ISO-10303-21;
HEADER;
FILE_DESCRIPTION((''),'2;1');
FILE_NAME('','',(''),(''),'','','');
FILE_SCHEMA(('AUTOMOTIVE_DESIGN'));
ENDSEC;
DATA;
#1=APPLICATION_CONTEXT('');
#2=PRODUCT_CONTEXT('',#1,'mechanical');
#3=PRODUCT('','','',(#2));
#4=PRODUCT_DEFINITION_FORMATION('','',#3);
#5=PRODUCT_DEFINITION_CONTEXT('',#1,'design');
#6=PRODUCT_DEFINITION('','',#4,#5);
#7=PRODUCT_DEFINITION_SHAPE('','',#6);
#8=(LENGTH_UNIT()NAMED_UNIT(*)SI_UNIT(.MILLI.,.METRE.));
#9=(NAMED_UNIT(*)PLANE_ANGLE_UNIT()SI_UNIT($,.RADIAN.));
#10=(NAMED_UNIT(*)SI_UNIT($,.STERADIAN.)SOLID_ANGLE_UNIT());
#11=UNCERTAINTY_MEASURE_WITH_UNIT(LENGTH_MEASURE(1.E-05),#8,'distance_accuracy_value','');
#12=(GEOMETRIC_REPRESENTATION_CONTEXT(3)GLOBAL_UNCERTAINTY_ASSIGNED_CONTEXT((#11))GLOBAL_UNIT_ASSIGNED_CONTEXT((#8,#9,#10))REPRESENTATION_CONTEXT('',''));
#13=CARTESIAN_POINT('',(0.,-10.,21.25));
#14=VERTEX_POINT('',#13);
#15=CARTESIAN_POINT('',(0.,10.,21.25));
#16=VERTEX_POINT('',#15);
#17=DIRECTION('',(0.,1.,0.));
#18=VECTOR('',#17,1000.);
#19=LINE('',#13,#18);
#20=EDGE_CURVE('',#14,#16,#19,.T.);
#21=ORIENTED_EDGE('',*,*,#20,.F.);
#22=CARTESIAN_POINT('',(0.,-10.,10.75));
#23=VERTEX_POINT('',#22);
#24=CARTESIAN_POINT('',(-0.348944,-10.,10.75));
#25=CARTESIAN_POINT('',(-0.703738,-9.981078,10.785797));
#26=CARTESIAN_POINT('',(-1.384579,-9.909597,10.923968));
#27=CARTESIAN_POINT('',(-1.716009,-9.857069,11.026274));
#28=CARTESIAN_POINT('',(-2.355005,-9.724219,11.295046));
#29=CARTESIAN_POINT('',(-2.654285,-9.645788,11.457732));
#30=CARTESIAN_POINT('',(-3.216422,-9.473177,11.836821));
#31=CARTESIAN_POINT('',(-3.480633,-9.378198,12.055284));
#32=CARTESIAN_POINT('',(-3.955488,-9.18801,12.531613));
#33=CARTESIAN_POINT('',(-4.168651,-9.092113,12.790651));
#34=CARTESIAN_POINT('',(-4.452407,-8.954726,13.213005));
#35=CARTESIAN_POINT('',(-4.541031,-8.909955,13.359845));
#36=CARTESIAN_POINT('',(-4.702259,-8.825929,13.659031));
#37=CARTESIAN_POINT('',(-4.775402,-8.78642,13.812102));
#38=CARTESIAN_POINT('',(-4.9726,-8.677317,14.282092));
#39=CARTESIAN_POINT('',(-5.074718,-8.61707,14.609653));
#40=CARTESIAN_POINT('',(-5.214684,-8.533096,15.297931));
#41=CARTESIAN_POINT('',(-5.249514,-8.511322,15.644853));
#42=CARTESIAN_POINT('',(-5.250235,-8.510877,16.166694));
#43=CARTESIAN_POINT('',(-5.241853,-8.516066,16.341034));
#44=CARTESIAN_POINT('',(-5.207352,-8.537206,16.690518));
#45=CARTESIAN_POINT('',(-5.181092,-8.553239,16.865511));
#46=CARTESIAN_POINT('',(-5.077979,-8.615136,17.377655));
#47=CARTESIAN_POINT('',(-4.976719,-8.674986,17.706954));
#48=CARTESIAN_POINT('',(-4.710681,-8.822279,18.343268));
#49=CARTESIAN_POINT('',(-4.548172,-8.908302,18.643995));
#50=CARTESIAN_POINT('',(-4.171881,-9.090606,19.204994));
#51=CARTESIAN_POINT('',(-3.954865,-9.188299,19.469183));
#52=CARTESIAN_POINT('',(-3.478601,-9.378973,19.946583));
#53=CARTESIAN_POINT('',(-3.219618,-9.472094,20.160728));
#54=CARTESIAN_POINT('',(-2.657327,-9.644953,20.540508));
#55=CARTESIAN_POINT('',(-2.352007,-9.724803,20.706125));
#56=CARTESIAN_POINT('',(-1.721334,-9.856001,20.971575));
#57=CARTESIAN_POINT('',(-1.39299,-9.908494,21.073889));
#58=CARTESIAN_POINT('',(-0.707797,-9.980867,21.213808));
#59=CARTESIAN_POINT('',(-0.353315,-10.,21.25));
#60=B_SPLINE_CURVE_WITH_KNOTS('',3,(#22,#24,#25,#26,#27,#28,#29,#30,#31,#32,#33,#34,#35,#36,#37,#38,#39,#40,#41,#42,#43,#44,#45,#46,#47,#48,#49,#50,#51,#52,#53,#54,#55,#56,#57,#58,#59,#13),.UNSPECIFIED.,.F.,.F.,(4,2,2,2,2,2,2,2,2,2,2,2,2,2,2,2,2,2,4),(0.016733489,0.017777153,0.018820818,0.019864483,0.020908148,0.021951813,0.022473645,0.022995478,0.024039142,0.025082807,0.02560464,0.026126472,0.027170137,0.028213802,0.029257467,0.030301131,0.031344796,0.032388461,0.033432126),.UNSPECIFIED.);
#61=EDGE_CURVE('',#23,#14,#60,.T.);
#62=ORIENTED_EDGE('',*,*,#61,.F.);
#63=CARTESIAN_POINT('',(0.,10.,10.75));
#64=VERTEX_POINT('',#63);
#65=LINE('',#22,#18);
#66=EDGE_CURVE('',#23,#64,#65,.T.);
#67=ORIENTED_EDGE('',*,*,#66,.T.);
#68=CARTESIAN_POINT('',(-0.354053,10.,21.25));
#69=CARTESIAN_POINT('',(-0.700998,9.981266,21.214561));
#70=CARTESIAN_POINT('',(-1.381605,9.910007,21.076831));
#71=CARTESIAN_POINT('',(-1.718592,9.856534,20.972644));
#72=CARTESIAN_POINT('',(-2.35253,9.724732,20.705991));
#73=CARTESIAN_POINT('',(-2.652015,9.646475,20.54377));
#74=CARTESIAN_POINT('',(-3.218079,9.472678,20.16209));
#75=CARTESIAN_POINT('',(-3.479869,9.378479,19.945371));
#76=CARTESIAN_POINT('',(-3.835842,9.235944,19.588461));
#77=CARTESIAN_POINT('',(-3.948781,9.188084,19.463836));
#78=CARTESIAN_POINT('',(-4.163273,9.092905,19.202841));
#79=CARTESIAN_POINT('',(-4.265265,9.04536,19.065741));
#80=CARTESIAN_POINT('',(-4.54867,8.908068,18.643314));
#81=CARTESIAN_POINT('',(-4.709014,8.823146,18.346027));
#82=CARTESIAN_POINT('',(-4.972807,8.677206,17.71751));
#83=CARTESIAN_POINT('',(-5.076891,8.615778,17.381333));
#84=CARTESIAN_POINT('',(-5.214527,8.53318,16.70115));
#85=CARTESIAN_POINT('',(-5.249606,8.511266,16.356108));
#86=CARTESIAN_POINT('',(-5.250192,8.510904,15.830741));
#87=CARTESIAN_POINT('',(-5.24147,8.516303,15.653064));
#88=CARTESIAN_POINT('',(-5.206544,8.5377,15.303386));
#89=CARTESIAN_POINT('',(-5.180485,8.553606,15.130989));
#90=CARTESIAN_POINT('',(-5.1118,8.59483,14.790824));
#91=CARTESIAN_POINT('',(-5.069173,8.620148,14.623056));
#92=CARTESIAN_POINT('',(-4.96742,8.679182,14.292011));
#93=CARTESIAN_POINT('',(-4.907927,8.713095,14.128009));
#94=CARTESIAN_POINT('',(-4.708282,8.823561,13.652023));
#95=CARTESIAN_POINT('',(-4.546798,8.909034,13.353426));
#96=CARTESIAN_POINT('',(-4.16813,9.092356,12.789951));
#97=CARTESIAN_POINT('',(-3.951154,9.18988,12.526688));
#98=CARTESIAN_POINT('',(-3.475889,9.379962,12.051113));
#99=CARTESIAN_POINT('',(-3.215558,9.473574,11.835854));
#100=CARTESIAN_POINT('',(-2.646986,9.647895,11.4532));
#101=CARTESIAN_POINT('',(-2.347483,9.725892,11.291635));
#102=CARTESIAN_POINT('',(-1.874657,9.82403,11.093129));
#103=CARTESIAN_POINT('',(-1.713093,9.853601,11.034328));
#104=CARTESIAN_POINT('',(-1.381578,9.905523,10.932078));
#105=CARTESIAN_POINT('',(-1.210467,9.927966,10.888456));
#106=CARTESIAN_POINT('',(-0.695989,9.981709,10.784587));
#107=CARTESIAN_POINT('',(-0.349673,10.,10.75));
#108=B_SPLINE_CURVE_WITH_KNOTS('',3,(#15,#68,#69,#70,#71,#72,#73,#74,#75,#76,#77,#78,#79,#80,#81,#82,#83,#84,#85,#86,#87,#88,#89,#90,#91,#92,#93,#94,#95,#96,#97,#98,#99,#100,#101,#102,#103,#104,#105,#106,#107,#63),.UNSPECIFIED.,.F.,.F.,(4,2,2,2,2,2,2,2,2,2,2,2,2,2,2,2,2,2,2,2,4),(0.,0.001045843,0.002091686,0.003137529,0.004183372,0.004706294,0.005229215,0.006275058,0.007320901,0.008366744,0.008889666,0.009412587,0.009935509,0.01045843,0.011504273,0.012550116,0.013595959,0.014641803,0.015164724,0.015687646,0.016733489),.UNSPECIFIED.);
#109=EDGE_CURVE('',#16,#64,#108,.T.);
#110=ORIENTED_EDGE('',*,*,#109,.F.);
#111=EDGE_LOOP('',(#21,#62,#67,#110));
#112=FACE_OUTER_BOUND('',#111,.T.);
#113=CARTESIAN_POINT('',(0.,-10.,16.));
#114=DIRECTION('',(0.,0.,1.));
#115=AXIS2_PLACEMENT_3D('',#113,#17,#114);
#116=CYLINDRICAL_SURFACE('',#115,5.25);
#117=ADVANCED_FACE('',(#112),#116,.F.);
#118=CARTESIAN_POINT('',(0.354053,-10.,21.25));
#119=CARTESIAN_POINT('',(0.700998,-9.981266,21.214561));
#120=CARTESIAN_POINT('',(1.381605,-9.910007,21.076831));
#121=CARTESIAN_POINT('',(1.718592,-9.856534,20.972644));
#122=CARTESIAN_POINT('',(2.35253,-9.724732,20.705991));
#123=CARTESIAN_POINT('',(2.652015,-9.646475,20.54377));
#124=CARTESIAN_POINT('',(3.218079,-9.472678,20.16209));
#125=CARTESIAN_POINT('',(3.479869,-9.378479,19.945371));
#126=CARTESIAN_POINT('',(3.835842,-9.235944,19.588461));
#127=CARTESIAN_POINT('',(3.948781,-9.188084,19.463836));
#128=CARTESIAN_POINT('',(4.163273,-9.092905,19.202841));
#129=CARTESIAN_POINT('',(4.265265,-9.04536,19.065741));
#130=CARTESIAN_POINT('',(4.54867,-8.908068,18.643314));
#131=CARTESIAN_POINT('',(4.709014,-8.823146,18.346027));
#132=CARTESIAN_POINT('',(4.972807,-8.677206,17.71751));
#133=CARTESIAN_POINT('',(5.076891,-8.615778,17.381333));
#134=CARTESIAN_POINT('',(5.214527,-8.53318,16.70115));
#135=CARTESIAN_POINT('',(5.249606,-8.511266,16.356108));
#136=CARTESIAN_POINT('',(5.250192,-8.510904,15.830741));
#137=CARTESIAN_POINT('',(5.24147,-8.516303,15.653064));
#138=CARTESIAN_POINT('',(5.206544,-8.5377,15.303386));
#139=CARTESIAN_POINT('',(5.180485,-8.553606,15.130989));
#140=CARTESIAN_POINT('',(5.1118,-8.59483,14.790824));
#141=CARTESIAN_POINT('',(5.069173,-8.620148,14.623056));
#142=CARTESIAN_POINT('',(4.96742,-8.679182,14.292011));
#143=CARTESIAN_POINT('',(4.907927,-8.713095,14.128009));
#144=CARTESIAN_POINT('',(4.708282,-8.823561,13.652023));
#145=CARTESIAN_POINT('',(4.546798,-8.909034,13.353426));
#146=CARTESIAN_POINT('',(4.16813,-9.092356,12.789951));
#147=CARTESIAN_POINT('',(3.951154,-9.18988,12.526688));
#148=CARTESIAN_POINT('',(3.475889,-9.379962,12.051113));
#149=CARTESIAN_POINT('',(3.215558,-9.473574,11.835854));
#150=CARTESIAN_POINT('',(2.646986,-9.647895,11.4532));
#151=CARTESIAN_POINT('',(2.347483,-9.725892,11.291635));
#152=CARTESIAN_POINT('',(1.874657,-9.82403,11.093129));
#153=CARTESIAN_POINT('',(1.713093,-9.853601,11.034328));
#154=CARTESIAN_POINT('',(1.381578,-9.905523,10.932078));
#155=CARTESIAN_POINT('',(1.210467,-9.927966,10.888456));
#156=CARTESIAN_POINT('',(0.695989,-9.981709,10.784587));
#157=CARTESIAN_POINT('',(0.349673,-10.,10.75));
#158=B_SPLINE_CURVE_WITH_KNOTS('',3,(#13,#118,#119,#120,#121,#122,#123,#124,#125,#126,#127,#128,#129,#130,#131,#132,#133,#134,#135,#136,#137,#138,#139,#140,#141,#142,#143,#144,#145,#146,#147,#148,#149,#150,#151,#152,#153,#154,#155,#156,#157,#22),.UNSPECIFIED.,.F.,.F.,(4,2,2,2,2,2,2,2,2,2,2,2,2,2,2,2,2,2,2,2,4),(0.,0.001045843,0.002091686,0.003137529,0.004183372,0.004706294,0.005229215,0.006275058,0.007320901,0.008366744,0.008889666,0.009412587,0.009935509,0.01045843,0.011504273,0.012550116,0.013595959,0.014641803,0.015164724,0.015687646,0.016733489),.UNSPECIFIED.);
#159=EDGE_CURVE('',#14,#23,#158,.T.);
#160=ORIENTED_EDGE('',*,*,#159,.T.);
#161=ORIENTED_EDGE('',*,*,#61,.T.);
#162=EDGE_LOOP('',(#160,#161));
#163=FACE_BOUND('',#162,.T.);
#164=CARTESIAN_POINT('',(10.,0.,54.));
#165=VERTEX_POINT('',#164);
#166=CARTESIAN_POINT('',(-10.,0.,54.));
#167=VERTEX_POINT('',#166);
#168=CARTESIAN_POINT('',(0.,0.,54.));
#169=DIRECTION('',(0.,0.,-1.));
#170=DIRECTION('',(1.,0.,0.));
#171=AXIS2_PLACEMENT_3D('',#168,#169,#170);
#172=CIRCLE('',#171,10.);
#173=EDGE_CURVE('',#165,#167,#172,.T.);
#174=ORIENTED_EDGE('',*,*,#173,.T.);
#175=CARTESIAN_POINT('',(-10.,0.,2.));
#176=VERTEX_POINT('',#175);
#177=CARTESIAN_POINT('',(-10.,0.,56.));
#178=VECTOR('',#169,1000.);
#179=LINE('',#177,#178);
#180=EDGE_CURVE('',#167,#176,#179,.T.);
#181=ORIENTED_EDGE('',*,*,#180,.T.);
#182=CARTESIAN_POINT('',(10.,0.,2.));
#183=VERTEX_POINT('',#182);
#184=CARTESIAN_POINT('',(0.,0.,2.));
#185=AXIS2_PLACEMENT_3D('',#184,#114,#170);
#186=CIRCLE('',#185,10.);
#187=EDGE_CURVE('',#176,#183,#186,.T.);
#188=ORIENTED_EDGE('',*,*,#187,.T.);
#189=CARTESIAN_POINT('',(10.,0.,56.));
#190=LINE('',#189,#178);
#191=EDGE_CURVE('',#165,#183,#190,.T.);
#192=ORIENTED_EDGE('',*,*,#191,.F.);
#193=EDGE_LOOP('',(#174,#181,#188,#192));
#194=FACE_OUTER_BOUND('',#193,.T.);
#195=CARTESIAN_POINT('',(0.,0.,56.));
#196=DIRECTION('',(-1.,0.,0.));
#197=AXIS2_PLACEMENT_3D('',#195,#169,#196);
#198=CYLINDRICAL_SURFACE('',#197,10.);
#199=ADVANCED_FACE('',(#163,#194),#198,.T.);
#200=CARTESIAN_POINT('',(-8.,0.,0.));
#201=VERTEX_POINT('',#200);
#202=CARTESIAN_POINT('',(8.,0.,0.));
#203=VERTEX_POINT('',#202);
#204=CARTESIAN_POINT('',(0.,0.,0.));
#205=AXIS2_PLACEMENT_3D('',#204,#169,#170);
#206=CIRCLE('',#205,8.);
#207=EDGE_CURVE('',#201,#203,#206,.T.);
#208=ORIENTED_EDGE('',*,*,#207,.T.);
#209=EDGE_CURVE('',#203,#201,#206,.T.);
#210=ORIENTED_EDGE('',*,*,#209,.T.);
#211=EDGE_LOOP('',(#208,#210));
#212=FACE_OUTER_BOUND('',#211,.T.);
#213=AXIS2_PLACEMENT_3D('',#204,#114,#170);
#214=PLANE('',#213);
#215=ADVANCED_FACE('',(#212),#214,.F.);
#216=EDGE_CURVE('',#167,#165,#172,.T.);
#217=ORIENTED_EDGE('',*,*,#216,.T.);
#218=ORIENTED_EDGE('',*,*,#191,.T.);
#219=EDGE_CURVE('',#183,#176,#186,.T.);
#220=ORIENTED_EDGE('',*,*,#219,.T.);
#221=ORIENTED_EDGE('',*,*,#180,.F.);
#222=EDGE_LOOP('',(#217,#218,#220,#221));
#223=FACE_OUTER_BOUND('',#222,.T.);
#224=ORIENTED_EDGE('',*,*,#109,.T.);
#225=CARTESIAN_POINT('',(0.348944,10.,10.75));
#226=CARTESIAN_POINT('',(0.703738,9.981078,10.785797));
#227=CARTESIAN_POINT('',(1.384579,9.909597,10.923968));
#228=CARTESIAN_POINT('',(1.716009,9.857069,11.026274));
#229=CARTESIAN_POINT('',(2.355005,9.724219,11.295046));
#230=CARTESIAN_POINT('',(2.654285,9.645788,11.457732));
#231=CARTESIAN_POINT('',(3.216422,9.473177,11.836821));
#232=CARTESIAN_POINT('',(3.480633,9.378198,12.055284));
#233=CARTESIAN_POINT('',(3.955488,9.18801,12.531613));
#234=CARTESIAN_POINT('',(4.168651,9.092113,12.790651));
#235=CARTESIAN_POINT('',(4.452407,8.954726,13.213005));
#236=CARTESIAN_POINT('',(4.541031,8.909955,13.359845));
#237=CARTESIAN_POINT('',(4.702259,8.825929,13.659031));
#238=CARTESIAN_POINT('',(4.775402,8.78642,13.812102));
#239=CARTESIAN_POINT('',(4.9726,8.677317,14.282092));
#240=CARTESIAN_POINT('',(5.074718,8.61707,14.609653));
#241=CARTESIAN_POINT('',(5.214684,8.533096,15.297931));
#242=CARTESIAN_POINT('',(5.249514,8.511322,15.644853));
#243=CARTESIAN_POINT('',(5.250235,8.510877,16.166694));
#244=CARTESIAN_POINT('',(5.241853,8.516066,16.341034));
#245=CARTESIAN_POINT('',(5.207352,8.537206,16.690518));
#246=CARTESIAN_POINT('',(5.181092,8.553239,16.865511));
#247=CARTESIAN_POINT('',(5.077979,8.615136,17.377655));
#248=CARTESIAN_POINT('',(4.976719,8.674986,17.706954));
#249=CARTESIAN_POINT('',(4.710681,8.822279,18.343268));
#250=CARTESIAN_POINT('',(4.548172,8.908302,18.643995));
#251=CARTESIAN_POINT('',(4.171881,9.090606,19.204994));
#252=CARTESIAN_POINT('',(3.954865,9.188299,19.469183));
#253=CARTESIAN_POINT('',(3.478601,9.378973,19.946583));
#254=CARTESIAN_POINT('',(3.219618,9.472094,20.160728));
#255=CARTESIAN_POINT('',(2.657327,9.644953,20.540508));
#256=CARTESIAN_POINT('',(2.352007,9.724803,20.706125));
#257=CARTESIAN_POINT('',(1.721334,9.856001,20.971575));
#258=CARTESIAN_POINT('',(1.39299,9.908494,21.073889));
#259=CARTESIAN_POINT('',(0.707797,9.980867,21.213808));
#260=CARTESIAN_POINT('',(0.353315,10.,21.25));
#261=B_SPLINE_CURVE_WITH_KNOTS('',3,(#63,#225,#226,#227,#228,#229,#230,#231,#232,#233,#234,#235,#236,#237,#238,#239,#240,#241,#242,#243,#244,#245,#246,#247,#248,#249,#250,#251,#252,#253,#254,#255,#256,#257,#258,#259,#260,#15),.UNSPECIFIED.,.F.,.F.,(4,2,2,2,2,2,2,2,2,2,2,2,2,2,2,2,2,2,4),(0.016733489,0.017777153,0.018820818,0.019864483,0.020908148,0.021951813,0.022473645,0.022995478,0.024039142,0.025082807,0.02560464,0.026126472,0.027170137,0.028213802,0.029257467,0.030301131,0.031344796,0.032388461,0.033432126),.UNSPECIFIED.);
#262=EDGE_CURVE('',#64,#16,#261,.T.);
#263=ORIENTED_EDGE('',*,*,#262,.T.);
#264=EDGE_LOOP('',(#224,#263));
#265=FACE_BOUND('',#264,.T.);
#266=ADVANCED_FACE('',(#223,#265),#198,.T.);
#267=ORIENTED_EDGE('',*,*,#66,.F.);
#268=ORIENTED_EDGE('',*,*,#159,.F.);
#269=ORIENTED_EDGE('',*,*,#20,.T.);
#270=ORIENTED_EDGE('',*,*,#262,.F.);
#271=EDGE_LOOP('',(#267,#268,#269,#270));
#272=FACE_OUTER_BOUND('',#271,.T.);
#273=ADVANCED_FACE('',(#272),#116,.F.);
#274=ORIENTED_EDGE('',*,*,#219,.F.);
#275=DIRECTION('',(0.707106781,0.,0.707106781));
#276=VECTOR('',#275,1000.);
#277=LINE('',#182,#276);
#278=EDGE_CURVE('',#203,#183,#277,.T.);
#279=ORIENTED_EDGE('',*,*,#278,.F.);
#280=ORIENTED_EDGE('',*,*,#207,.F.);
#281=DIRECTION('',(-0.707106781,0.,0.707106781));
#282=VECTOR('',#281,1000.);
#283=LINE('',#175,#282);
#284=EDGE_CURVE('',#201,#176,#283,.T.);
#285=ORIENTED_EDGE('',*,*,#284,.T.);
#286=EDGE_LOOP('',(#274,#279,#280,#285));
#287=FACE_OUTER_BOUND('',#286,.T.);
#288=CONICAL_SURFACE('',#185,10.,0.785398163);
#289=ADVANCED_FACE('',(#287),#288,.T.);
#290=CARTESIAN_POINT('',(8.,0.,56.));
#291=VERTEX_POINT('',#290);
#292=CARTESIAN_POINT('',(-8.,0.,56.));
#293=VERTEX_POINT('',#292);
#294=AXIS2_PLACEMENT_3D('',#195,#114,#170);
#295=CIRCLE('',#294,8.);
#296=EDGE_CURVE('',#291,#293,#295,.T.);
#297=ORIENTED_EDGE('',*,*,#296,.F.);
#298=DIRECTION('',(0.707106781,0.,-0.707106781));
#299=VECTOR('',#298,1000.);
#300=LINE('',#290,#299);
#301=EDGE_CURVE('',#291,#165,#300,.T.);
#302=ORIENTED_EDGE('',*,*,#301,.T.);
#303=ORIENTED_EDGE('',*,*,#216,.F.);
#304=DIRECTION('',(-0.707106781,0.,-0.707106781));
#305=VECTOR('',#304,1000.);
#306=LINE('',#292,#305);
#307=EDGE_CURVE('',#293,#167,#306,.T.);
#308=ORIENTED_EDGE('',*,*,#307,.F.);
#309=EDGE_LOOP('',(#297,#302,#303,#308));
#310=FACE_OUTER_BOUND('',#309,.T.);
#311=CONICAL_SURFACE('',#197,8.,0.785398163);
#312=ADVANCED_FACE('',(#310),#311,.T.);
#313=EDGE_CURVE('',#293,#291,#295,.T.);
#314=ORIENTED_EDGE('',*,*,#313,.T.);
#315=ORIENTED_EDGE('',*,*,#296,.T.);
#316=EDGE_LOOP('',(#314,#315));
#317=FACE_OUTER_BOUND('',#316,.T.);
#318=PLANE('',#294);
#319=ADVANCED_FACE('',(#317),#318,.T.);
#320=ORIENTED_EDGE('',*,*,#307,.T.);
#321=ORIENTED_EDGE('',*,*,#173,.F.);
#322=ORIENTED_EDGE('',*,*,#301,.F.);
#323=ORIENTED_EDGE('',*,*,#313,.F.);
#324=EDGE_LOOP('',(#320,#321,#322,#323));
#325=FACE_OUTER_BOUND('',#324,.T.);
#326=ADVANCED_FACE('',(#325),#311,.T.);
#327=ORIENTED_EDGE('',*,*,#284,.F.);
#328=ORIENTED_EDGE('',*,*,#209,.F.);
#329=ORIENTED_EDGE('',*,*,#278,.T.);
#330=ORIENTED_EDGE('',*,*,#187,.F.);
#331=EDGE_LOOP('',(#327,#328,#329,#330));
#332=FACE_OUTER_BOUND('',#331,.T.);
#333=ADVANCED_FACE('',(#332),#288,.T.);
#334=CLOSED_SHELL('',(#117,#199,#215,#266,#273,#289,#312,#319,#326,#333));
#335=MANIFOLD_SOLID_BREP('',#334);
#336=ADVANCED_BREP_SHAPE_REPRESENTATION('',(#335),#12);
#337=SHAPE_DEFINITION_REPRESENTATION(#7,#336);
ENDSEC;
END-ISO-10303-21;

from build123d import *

# Parameters (mm, degrees)
PIN_PROFILE_20_R         = 10
PIN_BODY_20X56_DEPTH     = 56
CROSS_HOLE_SKETCH_10_5_R = 5.25
CROSS_HOLE_10_5_DEPTH    = 10
END_CHAMFER_2X45_SIZE    = 2


with BuildPart() as part:
    # Pin Profile Ø20 → Pin Body Ø20x56 (new body)
    with BuildSketch(Plane.XY):
        Circle(PIN_PROFILE_20_R)
    extrude(amount=PIN_BODY_20X56_DEPTH)

    # Cross Hole Sketch Ø10.5 → Cross Hole Ø10.5 (cut, symmetric)
    with BuildSketch(Plane(origin=(0, 0, 0), x_dir=(1, 0, 0), z_dir=(0, 1, 0))):
        with Locations(Location((0, -16, 0), (0, 0, 270))):
            Circle(CROSS_HOLE_SKETCH_10_5_R)
    extrude(amount=CROSS_HOLE_10_5_DEPTH, both=True, mode=Mode.SUBTRACT)

    # End Chamfer 2x45°
    end_chamfer_2x45_edges = [part.edges().sort_by_distance(p)[0] for p in [
        (-10, 0, 0),
        (-10, 0, 56),
    ]]
    chamfer(end_chamfer_2x45_edges, length=END_CHAMFER_2X45_SIZE)


solid = part.part
